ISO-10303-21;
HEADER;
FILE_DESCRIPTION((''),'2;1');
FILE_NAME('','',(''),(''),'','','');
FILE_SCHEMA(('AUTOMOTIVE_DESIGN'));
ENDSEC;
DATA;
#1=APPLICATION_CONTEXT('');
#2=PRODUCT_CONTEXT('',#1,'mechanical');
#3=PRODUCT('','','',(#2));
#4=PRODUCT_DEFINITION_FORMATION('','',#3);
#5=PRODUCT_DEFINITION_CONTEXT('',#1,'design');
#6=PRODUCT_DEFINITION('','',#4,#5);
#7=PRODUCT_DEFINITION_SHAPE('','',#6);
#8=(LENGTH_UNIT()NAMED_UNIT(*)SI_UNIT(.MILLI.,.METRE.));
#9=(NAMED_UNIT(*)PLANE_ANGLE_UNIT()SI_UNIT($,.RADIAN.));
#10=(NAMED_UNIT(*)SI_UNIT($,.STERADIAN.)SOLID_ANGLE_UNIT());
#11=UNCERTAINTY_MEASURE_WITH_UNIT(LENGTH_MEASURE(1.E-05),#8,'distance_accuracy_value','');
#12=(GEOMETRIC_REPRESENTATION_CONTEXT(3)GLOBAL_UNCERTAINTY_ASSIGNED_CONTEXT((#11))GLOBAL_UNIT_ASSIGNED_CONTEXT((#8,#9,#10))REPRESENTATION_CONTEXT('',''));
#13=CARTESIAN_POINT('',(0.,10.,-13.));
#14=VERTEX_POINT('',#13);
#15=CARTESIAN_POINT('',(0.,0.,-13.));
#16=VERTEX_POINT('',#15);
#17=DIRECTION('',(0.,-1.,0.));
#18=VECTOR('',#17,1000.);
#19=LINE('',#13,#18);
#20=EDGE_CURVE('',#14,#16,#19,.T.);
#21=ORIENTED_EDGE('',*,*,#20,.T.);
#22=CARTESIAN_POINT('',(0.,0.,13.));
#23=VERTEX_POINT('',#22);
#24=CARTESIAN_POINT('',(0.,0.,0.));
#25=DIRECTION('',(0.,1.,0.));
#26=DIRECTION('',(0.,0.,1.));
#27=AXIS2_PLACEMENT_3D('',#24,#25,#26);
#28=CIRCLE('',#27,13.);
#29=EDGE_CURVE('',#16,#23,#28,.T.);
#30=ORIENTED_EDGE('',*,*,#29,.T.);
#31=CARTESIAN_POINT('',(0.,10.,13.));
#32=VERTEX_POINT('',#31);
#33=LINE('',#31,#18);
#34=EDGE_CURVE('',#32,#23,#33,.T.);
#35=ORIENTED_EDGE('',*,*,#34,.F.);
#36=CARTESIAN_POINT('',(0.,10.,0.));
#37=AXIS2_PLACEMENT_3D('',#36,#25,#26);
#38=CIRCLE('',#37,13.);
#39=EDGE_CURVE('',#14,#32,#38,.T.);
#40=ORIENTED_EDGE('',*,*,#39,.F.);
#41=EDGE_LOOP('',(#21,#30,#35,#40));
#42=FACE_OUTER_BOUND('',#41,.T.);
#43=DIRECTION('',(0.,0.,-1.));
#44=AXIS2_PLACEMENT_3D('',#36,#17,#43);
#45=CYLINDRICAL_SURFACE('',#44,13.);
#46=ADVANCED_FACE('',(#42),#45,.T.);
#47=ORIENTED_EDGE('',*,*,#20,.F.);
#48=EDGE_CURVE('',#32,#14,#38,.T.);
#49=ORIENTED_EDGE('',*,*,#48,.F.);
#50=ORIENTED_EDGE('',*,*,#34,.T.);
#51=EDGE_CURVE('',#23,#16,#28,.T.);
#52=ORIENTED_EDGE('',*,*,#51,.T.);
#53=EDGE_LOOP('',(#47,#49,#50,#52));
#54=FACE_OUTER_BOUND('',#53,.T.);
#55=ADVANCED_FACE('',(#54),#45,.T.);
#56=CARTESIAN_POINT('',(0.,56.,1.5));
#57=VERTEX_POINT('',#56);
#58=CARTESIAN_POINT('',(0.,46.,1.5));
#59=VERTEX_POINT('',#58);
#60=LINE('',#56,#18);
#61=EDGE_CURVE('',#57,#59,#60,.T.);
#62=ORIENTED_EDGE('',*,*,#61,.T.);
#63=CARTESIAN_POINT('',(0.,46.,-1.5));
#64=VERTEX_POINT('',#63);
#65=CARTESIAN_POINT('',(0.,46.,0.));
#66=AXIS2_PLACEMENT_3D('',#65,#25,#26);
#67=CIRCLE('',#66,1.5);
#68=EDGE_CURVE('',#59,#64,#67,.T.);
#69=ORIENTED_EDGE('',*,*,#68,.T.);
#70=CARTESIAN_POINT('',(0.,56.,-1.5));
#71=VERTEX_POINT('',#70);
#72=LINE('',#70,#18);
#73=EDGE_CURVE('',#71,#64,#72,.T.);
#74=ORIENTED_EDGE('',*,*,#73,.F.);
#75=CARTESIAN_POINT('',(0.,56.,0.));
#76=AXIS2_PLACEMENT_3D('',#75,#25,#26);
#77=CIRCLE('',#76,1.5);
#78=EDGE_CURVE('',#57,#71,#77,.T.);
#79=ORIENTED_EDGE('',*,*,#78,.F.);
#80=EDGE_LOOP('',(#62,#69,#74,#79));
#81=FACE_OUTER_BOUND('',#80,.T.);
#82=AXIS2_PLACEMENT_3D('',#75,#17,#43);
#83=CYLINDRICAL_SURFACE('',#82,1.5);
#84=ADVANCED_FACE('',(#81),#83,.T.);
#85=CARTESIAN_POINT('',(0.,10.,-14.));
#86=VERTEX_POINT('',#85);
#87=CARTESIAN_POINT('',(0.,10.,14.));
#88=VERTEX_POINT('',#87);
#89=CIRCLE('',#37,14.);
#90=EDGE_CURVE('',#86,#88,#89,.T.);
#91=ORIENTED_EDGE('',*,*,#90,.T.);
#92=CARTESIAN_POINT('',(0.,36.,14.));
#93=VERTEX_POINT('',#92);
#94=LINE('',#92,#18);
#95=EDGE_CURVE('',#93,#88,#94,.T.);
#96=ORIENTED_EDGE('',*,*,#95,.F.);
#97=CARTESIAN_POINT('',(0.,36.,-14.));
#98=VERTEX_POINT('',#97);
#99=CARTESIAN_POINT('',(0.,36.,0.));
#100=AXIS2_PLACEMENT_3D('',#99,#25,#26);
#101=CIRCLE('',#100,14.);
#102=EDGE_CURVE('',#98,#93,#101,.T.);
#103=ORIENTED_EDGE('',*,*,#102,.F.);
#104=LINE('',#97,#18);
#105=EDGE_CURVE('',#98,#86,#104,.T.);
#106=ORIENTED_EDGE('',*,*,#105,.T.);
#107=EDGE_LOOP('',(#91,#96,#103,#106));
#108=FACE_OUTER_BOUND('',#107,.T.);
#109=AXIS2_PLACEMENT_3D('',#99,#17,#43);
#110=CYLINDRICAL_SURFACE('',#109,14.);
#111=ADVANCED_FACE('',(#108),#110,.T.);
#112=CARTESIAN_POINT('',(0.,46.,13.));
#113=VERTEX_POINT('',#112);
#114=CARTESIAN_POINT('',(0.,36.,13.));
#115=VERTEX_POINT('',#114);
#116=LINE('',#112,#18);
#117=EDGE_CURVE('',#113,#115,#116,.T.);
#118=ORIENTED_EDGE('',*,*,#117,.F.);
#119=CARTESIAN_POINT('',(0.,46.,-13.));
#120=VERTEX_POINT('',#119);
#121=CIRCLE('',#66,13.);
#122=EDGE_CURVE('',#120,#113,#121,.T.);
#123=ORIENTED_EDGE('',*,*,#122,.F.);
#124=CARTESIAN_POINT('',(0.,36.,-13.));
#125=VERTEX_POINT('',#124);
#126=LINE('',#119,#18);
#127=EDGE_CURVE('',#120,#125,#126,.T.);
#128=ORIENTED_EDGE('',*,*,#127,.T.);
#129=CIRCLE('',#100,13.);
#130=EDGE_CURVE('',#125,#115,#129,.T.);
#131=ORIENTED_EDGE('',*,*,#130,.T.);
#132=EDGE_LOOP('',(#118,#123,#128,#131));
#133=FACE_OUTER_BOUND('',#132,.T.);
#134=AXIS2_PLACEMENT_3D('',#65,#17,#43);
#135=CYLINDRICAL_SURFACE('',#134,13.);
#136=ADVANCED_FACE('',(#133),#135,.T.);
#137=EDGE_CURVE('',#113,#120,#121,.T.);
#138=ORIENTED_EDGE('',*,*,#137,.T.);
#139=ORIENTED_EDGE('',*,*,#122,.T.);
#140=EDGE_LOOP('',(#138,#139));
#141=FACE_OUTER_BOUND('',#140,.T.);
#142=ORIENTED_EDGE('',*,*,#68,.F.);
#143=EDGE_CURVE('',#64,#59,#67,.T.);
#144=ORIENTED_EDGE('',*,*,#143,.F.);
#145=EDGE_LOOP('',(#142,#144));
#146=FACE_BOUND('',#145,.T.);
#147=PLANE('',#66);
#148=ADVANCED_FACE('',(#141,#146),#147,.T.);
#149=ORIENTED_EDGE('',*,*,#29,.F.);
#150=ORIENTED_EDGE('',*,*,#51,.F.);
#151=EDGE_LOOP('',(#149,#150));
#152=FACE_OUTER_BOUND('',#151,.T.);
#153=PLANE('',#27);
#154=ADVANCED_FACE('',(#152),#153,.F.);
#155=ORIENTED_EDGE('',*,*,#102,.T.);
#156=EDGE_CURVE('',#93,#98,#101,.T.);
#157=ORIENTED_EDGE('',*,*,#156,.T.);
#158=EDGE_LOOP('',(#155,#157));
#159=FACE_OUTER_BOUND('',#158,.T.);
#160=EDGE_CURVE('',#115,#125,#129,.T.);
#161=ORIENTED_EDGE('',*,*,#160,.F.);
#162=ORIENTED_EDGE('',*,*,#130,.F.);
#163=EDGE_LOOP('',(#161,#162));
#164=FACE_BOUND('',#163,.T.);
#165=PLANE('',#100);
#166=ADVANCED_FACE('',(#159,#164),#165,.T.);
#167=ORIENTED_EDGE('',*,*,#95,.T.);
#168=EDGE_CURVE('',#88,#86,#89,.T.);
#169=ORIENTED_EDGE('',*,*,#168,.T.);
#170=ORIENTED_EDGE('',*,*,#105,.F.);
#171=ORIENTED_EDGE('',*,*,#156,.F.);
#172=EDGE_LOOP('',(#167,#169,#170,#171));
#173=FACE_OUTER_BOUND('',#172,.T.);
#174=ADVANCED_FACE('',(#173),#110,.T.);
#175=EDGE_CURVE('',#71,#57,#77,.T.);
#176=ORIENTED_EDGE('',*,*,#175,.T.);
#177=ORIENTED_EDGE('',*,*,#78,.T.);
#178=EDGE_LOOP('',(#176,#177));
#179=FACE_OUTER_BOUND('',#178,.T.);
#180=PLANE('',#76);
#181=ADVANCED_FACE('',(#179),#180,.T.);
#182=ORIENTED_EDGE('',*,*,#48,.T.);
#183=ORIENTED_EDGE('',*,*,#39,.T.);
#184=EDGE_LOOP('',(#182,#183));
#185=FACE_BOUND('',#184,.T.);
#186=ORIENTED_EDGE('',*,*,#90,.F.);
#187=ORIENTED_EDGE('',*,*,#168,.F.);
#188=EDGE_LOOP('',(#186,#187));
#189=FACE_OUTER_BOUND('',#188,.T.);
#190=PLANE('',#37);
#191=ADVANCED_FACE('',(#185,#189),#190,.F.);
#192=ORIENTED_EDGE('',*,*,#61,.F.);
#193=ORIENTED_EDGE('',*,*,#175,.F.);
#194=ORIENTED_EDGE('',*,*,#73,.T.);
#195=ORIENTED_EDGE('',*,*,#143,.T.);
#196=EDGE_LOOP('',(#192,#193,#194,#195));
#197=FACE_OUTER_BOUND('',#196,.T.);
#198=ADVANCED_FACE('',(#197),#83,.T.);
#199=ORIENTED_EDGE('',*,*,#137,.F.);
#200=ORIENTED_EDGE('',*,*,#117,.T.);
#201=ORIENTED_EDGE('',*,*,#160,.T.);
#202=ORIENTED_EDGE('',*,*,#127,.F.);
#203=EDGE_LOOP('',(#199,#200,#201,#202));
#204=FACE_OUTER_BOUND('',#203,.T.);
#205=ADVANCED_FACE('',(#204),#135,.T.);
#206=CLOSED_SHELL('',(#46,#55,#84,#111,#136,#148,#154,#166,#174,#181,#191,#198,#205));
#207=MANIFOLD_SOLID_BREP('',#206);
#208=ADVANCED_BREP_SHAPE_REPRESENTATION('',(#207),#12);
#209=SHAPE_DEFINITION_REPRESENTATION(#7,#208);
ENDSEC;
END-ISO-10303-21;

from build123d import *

# Parameters (mm, degrees)
SKETCH1_R           = 13
BOSS_EXTRUDE1_DEPTH = 10
SKETCH2_R           = 14
BOSS_EXTRUDE2_DEPTH = 26
SKETCH3_R           = 13
BOSS_EXTRUDE3_DEPTH = 10
SKETCH4_R           = 1.5
BOSS_EXTRUDE4_DEPTH = 10


with BuildPart() as part:
    # Sketch1 → Boss-Extrude1 (new body)
    with BuildSketch(Plane(origin=(0, 0, 0), x_dir=(1, 0, 0), z_dir=(0, 1, 0))):
        with Locations(Location((0, 0, 0), (0, 0, 270))):
            Circle(SKETCH1_R)
    extrude(amount=BOSS_EXTRUDE1_DEPTH)

    # Sketch2 → Boss-Extrude2 (add)
    with BuildSketch(Plane(origin=(0, 10, 0), x_dir=(1, 0, 0), z_dir=(0, 1, 0))):
        with Locations(Location((0, 0, 0), (0, 0, 90))):
            Circle(SKETCH2_R)
    extrude(amount=BOSS_EXTRUDE2_DEPTH)

    # Sketch3 → Boss-Extrude3 (add)
    with BuildSketch(Plane(origin=(0, 36, 0), x_dir=(1, 0, 0), z_dir=(0, 1, 0))):
        with Locations(Location((0, 0, 0), (0, 0, 270))):
            Circle(SKETCH3_R)
    extrude(amount=BOSS_EXTRUDE3_DEPTH)

    # Sketch4 → Boss-Extrude4 (add)
    with BuildSketch(Plane(origin=(0, 46, 0), x_dir=(1, 0, 0), z_dir=(0, 1, 0))):
        with Locations(Location((0, 0, 0), (0, 0, 270))):
            Circle(SKETCH4_R)
    extrude(amount=BOSS_EXTRUDE4_DEPTH)


solid = part.part
